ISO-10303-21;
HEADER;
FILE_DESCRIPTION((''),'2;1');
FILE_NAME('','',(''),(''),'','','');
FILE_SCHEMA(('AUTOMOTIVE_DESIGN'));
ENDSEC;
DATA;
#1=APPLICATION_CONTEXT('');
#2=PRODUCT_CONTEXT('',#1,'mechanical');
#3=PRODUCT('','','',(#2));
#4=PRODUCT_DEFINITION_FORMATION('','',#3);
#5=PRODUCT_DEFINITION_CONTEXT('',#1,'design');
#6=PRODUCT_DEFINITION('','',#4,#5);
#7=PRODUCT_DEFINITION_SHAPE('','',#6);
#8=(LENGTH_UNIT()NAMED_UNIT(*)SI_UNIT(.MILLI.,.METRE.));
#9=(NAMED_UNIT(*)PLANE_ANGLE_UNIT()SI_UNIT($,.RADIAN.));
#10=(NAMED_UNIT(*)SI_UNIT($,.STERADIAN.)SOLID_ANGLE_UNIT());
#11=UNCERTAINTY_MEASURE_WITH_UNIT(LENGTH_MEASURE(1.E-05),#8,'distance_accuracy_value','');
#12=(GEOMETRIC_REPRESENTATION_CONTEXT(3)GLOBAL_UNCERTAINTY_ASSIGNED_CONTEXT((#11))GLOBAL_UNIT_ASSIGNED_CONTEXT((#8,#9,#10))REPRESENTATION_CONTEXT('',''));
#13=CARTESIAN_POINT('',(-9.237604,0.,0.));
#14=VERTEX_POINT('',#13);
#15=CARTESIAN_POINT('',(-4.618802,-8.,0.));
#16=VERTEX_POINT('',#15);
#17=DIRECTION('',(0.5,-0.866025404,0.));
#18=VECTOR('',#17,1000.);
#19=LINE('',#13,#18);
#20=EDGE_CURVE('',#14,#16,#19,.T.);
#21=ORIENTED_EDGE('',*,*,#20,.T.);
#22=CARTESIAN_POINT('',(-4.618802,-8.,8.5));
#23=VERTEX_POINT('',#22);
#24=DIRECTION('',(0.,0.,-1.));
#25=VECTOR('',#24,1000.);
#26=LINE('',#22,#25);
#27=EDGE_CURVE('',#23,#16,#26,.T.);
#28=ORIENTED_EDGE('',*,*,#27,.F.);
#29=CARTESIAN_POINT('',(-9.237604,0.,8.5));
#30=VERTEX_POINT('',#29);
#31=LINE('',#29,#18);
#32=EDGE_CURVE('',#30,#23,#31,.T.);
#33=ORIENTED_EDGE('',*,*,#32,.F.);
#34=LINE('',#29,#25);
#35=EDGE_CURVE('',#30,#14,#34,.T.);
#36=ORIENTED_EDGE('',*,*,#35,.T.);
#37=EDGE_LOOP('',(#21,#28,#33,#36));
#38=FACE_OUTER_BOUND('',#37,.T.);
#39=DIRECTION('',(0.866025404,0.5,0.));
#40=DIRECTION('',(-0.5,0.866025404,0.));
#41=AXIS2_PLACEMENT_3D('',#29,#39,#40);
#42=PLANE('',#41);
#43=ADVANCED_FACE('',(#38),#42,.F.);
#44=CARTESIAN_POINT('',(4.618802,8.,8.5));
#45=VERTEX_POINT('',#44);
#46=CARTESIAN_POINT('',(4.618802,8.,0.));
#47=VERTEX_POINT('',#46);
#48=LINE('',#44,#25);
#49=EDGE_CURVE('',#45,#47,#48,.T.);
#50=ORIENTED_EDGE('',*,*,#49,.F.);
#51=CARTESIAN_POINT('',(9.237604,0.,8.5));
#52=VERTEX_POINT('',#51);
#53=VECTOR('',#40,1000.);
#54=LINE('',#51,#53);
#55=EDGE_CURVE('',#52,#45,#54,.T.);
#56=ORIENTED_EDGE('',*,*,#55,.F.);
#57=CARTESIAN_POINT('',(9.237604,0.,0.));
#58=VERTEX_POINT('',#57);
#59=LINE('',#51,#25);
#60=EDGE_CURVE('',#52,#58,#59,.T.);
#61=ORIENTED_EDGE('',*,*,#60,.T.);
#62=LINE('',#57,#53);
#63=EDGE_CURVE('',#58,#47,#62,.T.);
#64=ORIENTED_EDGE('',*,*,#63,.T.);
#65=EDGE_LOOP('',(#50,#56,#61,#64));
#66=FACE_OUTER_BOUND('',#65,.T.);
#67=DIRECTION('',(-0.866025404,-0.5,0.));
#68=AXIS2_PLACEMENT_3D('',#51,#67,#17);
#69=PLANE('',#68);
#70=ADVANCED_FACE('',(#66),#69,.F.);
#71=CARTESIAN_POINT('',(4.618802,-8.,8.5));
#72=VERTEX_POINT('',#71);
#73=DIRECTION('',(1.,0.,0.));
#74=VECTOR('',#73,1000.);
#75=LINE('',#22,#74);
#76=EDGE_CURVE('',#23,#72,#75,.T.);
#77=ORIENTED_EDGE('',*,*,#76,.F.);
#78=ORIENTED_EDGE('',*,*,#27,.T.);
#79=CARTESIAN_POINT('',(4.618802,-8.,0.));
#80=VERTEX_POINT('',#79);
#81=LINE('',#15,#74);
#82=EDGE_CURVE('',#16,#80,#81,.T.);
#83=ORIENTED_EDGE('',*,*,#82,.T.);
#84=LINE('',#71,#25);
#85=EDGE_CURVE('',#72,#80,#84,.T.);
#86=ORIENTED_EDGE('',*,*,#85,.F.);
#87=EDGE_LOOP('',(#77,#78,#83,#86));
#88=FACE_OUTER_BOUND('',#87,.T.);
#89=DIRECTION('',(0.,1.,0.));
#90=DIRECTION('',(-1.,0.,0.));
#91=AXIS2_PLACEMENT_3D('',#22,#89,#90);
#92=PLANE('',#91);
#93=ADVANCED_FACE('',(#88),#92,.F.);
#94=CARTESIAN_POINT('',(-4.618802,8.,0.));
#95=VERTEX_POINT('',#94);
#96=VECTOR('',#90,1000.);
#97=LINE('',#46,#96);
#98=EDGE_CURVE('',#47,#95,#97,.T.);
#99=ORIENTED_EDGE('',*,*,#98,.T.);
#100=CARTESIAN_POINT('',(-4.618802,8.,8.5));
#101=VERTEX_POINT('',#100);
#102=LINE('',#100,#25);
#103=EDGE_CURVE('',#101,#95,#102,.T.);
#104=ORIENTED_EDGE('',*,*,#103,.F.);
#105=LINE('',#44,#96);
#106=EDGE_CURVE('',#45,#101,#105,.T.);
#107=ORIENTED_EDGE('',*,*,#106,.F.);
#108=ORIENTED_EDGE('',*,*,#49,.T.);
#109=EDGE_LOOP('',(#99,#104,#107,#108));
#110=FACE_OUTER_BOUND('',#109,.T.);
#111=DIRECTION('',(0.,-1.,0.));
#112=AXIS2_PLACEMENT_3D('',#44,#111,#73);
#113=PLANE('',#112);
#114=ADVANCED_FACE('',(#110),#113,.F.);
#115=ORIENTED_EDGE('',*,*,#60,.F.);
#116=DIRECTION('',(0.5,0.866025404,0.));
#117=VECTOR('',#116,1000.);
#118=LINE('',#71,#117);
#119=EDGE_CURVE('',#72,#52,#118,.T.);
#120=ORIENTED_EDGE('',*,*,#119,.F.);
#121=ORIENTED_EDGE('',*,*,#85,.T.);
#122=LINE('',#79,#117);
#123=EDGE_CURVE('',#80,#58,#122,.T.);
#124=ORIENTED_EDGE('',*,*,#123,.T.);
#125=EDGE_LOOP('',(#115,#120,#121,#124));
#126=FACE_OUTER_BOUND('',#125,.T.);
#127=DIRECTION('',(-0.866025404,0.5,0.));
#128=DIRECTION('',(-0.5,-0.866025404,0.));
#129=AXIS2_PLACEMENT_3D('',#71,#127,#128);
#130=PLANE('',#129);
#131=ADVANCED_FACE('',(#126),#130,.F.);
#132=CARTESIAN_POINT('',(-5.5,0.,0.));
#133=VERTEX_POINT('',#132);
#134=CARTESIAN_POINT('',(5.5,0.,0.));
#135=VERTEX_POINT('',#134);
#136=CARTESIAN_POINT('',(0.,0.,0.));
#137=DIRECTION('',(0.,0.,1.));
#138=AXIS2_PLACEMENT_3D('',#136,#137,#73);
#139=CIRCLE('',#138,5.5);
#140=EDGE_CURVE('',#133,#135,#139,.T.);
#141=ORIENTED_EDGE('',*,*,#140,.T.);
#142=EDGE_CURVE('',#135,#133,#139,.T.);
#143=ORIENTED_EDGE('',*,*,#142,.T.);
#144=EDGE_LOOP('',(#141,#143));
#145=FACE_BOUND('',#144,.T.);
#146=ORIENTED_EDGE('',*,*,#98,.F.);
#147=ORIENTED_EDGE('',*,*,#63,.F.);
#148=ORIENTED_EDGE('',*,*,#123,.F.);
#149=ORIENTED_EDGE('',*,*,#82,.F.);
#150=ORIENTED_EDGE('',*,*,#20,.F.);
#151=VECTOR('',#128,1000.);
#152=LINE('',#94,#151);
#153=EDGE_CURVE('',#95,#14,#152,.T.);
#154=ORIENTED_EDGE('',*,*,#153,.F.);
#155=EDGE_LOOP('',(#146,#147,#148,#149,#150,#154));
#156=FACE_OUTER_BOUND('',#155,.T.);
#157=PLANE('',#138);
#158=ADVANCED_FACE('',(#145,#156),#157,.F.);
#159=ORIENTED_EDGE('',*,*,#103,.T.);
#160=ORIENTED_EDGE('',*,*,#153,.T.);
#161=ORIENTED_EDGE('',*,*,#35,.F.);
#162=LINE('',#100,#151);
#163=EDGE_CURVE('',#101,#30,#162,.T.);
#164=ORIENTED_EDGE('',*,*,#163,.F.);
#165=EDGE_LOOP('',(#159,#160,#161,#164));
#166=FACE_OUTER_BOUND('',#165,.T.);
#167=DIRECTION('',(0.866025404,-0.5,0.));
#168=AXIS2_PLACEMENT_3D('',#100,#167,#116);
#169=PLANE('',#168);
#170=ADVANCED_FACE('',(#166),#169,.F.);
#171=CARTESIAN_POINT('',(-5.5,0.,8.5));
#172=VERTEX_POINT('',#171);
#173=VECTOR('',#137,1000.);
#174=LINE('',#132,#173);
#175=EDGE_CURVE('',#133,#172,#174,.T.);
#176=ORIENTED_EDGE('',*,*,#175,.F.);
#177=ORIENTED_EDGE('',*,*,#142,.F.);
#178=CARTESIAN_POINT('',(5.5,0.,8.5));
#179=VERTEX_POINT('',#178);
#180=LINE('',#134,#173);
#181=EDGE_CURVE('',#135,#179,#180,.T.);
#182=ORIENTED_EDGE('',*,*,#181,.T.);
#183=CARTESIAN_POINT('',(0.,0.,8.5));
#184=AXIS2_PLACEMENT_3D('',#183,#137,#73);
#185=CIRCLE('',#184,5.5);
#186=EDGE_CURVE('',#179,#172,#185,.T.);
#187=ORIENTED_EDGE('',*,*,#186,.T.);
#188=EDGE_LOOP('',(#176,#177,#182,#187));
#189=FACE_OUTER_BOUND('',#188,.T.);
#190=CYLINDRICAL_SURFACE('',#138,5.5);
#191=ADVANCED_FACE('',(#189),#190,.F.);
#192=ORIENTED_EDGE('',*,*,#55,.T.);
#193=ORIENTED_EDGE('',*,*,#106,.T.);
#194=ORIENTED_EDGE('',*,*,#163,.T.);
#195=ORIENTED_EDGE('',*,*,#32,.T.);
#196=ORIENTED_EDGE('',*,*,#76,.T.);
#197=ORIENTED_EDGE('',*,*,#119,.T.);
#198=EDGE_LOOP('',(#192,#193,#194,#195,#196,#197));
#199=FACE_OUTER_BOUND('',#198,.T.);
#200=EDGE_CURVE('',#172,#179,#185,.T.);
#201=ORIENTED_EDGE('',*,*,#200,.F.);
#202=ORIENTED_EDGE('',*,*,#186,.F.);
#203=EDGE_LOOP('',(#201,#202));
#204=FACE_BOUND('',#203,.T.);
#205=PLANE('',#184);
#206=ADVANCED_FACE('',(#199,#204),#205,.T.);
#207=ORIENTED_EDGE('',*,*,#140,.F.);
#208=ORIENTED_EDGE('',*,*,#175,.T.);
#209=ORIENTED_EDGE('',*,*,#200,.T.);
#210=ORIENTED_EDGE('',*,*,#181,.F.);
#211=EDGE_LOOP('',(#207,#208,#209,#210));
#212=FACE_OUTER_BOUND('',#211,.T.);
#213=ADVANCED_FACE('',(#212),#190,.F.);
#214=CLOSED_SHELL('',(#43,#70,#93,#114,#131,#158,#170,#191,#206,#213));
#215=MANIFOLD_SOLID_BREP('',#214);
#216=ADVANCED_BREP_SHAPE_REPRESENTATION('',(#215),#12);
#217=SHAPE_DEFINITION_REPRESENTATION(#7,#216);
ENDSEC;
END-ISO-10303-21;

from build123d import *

# Parameters (mm, degrees)
EXTRUDE_1_DEPTH     = 8.5
SKETCH_2_R          = 5.5
CUT_EXTRUDE_1_DEPTH = 8.5


with BuildPart() as part:
    # 草图1 → 凸台-拉伸1 (new body)
    with BuildSketch(Plane.XY):
        Polygon((9.237604307, 0), (4.618802154, 8), (-4.618802154, 8), (-9.237604307, 0), (-4.618802154, -8), (4.618802154, -8), align=None)
    extrude(amount=EXTRUDE_1_DEPTH)

    # 草图2 → 切除-拉伸1 (cut)
    with BuildSketch(Plane.XY.offset(8.5)):
        Circle(SKETCH_2_R)
    extrude(amount=-CUT_EXTRUDE_1_DEPTH, mode=Mode.SUBTRACT)


solid = part.part
